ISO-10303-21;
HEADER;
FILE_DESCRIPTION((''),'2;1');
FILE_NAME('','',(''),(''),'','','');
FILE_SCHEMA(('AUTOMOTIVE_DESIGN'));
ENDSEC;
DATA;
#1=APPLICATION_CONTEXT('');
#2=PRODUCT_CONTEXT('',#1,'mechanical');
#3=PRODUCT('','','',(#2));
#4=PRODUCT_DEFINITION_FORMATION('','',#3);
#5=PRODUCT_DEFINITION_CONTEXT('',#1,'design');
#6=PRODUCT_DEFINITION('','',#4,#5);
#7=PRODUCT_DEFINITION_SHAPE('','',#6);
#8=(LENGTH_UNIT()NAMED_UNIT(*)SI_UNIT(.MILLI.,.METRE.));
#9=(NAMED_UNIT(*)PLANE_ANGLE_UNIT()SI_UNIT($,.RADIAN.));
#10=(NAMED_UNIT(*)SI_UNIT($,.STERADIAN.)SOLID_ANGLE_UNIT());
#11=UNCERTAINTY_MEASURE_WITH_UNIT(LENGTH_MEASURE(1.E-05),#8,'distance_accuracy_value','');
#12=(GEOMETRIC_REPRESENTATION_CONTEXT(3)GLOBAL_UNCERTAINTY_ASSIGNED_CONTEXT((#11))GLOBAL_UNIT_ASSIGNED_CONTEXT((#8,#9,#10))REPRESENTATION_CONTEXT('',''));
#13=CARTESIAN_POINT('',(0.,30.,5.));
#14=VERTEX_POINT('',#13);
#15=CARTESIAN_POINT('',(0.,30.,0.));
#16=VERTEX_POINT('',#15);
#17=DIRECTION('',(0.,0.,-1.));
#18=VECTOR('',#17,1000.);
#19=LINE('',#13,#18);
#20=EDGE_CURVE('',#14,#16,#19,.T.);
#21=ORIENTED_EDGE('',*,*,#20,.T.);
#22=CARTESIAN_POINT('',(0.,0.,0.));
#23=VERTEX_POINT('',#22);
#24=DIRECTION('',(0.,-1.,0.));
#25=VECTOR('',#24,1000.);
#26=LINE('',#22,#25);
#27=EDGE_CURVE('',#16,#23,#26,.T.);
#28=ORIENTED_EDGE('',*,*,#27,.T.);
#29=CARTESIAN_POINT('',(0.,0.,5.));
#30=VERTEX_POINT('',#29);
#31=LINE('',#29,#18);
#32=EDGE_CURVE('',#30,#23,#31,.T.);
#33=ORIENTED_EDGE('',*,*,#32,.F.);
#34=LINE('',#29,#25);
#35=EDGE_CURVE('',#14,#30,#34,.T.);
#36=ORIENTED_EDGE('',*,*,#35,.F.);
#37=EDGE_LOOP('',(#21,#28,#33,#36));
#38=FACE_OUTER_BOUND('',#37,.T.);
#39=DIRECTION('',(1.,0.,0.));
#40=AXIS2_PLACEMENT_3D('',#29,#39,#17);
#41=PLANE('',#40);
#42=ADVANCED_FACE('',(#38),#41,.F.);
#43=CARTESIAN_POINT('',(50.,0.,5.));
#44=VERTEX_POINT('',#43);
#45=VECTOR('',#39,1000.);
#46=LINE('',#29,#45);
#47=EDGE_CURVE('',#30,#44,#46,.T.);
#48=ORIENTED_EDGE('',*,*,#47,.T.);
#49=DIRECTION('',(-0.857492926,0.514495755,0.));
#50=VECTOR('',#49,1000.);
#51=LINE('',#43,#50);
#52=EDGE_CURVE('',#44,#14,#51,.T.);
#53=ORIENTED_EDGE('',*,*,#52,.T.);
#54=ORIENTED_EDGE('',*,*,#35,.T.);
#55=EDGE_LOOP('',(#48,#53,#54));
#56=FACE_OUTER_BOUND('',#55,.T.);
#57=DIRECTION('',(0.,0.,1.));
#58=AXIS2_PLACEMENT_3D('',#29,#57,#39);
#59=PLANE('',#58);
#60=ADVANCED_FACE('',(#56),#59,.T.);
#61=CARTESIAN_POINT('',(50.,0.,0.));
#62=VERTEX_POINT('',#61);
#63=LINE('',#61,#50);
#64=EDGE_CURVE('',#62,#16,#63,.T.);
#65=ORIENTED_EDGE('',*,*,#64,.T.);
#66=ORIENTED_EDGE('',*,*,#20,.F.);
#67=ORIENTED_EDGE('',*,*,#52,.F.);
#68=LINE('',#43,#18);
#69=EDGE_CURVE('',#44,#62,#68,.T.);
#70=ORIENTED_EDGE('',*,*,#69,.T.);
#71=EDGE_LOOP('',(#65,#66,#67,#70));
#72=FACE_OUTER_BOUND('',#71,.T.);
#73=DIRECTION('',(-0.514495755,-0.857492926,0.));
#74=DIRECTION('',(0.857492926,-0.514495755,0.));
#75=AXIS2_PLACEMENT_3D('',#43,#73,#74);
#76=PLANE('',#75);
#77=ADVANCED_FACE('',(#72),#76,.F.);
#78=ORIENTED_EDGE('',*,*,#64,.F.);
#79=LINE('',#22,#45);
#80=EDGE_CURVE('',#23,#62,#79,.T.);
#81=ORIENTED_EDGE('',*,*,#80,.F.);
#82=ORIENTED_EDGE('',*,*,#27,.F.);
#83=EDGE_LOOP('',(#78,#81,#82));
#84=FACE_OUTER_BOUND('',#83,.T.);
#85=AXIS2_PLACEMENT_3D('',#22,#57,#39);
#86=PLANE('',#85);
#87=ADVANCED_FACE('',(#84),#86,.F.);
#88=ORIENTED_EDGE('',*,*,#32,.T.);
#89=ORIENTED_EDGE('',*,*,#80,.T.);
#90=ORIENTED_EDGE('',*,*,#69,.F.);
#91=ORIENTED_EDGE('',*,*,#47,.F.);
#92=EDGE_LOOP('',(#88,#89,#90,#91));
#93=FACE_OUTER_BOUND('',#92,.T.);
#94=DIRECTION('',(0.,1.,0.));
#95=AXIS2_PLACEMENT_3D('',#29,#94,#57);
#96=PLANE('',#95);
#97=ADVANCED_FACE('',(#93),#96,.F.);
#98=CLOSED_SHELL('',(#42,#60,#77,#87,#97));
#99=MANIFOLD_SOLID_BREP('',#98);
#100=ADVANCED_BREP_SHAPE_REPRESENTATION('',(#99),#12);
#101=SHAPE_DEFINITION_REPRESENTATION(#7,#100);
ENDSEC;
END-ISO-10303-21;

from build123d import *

# Parameters (mm, degrees)
EXTRUDE_1_DEPTH = 5


with BuildPart() as part:
    # 草图1 → 凸台-拉伸1 (new body)
    with BuildSketch(Plane.XY):
        Polygon((0, 0), (0, 30), (50, 0), align=None)
    extrude(amount=EXTRUDE_1_DEPTH)


solid = part.part
